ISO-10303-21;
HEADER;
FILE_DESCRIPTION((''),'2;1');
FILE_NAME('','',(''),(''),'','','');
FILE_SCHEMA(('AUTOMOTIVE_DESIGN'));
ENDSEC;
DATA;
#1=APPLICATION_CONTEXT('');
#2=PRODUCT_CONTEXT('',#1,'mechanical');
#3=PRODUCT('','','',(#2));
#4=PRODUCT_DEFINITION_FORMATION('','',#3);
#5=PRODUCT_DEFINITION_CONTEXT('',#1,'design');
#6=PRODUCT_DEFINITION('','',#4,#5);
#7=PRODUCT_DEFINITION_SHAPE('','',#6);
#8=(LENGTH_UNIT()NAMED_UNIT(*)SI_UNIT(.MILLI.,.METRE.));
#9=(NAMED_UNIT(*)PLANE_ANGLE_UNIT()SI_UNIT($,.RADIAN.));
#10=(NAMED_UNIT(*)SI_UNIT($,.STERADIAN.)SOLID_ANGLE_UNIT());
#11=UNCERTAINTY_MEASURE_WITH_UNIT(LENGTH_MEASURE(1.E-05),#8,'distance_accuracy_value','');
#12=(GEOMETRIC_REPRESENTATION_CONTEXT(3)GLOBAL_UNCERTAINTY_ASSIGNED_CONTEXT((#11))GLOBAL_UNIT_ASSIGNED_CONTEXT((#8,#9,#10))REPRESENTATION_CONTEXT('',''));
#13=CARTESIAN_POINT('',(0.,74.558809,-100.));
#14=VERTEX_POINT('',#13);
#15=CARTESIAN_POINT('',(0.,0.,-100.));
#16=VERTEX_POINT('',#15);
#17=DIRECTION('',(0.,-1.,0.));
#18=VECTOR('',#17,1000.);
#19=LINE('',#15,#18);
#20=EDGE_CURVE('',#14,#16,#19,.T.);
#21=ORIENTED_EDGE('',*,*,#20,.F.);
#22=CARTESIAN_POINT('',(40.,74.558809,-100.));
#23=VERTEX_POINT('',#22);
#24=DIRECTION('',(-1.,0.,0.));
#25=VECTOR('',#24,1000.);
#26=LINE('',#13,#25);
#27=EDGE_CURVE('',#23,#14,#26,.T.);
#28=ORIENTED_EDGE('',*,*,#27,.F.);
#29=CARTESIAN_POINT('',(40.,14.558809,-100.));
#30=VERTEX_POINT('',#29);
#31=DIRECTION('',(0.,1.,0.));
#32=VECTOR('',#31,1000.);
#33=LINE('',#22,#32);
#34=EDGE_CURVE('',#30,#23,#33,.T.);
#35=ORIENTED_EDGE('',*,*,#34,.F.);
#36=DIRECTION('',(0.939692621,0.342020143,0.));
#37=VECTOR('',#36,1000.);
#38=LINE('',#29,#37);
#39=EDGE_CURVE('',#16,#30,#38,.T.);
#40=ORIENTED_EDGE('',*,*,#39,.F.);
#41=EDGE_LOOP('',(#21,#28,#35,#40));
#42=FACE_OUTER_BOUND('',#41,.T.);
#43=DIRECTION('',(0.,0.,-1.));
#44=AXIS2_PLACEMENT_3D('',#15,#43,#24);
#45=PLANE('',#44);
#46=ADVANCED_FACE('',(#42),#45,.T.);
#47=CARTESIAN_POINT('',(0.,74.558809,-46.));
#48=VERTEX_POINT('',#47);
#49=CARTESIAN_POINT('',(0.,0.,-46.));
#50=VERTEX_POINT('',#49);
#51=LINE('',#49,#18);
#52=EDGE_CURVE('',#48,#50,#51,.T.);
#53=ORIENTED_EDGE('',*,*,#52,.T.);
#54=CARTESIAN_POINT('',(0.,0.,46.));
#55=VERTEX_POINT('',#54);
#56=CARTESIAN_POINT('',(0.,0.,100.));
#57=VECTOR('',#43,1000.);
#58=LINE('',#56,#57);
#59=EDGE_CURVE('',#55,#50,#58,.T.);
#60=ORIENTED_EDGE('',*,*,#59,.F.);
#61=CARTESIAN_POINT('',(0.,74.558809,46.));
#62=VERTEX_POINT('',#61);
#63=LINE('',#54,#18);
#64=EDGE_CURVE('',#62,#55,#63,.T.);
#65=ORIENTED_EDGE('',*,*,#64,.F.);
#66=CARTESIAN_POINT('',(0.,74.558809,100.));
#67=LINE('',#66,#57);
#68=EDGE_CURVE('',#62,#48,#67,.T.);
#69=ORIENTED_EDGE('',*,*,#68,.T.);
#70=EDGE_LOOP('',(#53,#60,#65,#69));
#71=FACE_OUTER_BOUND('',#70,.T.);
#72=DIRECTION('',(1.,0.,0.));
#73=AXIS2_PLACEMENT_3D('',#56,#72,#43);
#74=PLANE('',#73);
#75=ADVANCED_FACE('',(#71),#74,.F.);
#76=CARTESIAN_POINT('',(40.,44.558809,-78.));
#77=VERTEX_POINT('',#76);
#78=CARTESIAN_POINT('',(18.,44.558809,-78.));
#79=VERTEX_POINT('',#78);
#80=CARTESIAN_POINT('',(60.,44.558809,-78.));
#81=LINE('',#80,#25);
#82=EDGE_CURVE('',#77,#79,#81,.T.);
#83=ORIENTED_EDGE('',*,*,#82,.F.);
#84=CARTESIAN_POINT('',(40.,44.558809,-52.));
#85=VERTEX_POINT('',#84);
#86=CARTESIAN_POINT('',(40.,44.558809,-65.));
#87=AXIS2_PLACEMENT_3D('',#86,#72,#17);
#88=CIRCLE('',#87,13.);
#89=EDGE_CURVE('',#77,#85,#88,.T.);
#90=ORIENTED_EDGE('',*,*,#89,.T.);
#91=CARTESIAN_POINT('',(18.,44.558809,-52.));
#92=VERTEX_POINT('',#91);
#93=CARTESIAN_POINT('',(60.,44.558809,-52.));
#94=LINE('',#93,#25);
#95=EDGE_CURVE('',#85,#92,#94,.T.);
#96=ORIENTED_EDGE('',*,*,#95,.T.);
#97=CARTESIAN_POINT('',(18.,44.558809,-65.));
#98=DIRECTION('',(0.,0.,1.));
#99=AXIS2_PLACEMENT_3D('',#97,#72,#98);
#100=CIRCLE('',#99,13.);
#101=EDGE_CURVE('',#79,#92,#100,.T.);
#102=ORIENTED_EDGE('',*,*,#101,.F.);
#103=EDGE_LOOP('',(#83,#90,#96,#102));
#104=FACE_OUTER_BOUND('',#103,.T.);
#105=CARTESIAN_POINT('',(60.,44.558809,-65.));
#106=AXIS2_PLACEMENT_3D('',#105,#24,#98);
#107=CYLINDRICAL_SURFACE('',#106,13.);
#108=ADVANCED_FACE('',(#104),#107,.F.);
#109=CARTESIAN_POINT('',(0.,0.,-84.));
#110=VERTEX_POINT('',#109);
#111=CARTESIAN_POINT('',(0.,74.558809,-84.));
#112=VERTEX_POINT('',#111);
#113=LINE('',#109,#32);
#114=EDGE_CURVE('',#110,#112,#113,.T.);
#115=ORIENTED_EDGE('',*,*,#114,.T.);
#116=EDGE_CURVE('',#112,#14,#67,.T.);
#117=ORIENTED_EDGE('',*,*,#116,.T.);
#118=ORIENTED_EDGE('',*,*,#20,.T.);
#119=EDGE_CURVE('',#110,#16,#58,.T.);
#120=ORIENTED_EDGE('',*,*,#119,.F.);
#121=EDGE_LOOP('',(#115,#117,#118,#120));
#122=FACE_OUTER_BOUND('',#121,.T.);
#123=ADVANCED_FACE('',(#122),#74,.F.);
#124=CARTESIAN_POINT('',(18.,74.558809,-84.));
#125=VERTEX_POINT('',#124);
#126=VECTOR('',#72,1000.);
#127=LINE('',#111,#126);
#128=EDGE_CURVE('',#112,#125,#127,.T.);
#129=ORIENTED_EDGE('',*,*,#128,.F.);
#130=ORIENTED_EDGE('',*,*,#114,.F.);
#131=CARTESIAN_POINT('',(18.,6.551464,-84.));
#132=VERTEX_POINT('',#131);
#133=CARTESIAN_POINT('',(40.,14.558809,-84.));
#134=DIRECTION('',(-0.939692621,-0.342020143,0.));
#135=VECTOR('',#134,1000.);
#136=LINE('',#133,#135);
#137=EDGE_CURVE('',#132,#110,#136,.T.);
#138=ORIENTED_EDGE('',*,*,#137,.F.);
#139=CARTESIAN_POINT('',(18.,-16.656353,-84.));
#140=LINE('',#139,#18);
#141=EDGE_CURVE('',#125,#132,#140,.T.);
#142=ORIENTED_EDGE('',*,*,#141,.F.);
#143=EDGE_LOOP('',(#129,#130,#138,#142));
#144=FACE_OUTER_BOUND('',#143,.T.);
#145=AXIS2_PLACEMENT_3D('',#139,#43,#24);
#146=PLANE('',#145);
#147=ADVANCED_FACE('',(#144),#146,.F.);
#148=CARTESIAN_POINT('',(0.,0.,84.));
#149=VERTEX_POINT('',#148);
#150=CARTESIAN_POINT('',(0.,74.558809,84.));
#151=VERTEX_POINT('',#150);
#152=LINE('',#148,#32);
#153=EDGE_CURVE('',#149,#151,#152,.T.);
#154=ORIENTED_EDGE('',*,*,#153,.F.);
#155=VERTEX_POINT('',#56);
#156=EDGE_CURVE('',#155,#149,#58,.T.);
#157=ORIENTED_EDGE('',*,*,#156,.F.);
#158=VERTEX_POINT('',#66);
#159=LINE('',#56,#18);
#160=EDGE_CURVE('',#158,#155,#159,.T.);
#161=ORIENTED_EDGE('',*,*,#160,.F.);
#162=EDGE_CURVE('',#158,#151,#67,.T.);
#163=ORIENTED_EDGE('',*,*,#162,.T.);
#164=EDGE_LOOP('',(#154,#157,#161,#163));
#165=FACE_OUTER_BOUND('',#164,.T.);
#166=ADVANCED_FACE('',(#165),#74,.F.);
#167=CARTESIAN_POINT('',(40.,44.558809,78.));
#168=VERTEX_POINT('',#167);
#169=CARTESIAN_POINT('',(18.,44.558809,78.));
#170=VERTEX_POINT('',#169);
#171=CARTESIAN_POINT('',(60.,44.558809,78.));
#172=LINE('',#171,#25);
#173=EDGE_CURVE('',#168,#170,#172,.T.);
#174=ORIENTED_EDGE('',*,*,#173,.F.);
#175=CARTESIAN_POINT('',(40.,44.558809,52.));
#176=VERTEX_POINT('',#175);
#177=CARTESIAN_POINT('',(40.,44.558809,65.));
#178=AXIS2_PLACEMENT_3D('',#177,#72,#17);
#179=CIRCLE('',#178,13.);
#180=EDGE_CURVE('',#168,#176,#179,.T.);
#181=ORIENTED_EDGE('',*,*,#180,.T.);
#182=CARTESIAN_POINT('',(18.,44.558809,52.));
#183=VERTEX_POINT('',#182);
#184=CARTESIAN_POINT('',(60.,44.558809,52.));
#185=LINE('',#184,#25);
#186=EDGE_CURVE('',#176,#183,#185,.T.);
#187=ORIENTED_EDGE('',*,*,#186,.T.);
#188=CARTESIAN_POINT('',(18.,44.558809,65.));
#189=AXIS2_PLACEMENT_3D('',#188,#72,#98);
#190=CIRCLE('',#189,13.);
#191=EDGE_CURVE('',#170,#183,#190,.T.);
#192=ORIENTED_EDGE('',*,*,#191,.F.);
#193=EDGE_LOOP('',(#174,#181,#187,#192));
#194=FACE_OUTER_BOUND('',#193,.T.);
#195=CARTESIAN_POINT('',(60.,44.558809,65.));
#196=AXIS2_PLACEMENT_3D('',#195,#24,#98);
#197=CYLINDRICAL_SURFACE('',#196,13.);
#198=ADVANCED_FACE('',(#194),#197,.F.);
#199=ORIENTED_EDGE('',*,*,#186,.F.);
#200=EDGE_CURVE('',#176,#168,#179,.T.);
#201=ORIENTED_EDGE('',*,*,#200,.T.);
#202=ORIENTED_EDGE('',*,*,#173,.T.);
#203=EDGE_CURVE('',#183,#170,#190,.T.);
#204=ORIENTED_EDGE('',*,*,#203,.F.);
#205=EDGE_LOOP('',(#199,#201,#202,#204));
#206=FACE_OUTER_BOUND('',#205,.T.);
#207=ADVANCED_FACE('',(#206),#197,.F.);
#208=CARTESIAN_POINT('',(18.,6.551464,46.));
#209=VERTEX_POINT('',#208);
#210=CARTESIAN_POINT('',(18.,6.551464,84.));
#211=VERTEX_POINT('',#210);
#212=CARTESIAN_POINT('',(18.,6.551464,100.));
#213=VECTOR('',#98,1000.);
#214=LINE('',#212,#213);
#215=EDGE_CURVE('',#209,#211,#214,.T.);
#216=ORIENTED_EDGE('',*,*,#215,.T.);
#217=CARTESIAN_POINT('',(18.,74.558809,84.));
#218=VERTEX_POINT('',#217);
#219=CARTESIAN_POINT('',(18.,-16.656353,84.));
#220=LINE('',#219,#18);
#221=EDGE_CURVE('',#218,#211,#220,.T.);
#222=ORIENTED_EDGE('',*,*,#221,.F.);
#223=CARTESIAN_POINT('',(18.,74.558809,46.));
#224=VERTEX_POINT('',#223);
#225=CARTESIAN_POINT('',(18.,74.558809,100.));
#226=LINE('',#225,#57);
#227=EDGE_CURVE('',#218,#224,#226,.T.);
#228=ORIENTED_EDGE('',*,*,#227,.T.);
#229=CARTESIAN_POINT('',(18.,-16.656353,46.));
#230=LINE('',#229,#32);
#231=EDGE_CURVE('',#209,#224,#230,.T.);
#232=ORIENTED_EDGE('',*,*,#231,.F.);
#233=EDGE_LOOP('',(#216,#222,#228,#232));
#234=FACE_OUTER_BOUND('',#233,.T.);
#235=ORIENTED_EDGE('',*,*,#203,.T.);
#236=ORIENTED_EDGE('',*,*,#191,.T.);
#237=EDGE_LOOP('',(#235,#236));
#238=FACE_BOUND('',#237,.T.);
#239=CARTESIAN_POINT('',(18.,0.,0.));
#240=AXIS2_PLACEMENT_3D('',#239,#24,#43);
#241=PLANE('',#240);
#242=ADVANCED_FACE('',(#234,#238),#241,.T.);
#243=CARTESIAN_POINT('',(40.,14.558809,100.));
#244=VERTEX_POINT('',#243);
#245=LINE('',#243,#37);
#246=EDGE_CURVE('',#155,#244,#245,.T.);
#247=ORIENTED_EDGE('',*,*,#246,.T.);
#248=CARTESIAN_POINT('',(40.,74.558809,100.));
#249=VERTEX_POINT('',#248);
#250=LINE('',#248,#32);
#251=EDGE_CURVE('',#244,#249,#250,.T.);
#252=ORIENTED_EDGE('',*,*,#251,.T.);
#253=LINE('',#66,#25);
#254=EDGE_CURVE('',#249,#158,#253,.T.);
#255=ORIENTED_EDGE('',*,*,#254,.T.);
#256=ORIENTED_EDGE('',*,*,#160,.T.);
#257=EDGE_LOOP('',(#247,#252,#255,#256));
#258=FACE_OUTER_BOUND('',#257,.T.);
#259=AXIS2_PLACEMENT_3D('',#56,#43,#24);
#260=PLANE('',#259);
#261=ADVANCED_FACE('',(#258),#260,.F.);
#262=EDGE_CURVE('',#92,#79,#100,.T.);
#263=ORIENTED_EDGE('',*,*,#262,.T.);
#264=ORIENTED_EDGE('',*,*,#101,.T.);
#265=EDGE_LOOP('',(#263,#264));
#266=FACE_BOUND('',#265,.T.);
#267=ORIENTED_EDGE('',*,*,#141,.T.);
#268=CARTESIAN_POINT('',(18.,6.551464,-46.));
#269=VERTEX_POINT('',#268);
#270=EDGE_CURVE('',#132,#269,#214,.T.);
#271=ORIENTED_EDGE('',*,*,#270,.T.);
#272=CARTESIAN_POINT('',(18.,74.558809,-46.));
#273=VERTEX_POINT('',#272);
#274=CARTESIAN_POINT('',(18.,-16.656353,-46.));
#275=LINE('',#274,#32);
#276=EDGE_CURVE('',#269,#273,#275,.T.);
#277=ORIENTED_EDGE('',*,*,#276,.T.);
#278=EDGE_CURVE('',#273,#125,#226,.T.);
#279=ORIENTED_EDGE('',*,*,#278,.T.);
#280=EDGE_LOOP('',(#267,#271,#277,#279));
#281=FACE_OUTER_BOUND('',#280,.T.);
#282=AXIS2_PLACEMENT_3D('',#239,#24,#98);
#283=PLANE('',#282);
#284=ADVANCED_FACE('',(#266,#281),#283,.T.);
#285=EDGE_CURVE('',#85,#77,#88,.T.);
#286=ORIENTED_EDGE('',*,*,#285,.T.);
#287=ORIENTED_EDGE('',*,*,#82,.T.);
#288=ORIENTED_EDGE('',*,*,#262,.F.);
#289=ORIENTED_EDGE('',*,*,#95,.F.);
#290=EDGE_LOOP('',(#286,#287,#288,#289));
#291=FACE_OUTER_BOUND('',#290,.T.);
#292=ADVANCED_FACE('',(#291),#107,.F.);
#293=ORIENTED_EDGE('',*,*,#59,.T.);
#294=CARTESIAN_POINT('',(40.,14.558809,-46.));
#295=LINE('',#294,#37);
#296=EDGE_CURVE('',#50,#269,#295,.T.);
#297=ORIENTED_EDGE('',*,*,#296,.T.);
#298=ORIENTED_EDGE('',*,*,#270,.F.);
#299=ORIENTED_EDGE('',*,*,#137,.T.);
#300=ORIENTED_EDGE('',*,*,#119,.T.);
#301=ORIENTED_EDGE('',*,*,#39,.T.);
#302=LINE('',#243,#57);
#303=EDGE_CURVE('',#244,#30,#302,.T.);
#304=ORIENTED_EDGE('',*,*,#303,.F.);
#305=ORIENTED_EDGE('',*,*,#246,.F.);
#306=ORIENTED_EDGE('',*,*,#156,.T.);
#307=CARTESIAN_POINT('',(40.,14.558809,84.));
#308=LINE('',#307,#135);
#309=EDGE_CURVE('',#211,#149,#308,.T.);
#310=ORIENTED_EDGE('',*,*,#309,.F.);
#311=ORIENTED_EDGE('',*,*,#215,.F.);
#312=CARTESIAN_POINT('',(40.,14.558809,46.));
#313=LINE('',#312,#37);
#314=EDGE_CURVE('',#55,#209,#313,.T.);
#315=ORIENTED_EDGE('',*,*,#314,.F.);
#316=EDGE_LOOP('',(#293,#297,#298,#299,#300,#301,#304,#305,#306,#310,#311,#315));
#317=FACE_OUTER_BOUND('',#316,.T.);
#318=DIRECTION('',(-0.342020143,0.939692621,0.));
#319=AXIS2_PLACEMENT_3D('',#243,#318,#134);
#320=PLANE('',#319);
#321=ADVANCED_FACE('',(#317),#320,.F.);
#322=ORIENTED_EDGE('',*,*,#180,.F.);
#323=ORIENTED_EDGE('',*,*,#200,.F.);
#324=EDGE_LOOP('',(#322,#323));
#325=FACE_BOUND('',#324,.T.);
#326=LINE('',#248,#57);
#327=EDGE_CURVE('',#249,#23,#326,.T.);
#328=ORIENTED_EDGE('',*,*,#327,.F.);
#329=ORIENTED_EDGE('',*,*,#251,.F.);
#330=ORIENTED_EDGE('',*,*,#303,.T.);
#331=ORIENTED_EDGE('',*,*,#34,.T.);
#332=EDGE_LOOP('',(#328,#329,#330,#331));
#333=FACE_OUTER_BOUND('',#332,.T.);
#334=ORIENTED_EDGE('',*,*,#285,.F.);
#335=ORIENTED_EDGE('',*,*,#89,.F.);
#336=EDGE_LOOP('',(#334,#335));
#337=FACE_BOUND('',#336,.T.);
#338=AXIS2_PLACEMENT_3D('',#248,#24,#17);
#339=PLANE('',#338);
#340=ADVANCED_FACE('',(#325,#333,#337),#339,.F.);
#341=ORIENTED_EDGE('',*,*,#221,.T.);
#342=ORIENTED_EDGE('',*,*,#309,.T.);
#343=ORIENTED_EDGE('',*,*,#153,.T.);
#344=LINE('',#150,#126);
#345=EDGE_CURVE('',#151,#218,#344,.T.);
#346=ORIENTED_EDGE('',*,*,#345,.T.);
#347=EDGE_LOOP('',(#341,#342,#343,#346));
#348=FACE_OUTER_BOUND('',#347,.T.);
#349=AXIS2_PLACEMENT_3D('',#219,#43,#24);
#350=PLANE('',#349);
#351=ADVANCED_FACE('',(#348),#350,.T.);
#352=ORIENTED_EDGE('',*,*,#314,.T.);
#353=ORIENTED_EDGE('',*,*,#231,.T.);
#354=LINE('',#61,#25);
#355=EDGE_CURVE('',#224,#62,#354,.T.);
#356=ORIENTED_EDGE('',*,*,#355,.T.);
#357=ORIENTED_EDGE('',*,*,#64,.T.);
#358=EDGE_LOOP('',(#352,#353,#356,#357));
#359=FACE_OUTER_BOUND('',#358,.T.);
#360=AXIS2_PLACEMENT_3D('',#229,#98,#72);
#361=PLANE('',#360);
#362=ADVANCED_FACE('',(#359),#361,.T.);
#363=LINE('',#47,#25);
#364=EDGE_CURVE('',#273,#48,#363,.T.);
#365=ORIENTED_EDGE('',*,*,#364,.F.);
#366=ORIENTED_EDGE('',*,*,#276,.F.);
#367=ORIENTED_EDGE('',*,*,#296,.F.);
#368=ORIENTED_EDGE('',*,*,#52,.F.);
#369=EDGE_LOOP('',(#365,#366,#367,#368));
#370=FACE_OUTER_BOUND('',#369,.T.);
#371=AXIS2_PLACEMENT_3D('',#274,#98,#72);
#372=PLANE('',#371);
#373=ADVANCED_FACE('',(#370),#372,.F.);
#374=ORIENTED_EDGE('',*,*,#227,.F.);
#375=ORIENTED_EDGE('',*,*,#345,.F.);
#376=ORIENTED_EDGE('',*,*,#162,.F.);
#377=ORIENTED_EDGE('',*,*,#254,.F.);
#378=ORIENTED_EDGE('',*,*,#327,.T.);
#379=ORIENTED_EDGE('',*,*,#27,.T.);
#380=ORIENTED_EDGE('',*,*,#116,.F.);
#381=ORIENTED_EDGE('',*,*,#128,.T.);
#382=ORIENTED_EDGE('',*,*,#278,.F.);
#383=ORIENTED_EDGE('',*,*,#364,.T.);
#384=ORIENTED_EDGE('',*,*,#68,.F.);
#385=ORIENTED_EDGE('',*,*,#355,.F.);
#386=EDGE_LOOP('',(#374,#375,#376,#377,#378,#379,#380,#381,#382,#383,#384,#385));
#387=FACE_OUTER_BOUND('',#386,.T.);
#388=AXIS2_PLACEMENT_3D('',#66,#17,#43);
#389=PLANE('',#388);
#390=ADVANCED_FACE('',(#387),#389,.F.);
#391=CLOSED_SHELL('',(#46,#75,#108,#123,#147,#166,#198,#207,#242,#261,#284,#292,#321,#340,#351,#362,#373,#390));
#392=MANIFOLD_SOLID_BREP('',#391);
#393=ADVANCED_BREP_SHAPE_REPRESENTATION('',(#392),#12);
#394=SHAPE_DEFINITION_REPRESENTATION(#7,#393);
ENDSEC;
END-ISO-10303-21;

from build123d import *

# Parameters (mm, degrees)
BOSS_EXTRUDE1_DEPTH = 100
SKETCH3_W           = 38
SKETCH3_H           = 122.430323754
CUT_EXTRUDE1_DEPTH  = 18
SKETCH4_R           = 13
CUT_EXTRUDE2_DEPTH  = 60


with BuildPart() as part:
    # Sketch2 → Boss-Extrude1 (new, symmetric)
    with BuildSketch(Plane.XY):
        Polygon((0, 0), (0, 74.558809371), (40, 74.558809371), (40, 14.558809371), align=None)
    extrude(amount=BOSS_EXTRUDE1_DEPTH, both=True)

    # Sketch3 → Cut-Extrude1 (cut)
    with BuildSketch(Plane.ZY):
        with Locations((-65, 44.558809371)):
            Rectangle(SKETCH3_W, SKETCH3_H)
    cut_extrude1 = extrude(amount=-CUT_EXTRUDE1_DEPTH, mode=Mode.SUBTRACT)

    # Mirror1: Cut-Extrude1 across plane
    add(cut_extrude1.mirror(Plane.XY), mode=Mode.SUBTRACT)

    # Sketch4 → Cut-Extrude2 (cut)
    with BuildSketch(Plane(origin=(0, 0, 0), x_dir=(0, 0, -1), z_dir=(1, 0, 0))):
        with Locations(Location((65, 44.558809371, 0), (0, 0, 180))):
            Circle(SKETCH4_R)
        with Locations(Location((-65, 44.558809371, 0), (0, 0, 180))):
            Circle(SKETCH4_R)
    extrude(amount=CUT_EXTRUDE2_DEPTH, mode=Mode.SUBTRACT)


solid = part.part
